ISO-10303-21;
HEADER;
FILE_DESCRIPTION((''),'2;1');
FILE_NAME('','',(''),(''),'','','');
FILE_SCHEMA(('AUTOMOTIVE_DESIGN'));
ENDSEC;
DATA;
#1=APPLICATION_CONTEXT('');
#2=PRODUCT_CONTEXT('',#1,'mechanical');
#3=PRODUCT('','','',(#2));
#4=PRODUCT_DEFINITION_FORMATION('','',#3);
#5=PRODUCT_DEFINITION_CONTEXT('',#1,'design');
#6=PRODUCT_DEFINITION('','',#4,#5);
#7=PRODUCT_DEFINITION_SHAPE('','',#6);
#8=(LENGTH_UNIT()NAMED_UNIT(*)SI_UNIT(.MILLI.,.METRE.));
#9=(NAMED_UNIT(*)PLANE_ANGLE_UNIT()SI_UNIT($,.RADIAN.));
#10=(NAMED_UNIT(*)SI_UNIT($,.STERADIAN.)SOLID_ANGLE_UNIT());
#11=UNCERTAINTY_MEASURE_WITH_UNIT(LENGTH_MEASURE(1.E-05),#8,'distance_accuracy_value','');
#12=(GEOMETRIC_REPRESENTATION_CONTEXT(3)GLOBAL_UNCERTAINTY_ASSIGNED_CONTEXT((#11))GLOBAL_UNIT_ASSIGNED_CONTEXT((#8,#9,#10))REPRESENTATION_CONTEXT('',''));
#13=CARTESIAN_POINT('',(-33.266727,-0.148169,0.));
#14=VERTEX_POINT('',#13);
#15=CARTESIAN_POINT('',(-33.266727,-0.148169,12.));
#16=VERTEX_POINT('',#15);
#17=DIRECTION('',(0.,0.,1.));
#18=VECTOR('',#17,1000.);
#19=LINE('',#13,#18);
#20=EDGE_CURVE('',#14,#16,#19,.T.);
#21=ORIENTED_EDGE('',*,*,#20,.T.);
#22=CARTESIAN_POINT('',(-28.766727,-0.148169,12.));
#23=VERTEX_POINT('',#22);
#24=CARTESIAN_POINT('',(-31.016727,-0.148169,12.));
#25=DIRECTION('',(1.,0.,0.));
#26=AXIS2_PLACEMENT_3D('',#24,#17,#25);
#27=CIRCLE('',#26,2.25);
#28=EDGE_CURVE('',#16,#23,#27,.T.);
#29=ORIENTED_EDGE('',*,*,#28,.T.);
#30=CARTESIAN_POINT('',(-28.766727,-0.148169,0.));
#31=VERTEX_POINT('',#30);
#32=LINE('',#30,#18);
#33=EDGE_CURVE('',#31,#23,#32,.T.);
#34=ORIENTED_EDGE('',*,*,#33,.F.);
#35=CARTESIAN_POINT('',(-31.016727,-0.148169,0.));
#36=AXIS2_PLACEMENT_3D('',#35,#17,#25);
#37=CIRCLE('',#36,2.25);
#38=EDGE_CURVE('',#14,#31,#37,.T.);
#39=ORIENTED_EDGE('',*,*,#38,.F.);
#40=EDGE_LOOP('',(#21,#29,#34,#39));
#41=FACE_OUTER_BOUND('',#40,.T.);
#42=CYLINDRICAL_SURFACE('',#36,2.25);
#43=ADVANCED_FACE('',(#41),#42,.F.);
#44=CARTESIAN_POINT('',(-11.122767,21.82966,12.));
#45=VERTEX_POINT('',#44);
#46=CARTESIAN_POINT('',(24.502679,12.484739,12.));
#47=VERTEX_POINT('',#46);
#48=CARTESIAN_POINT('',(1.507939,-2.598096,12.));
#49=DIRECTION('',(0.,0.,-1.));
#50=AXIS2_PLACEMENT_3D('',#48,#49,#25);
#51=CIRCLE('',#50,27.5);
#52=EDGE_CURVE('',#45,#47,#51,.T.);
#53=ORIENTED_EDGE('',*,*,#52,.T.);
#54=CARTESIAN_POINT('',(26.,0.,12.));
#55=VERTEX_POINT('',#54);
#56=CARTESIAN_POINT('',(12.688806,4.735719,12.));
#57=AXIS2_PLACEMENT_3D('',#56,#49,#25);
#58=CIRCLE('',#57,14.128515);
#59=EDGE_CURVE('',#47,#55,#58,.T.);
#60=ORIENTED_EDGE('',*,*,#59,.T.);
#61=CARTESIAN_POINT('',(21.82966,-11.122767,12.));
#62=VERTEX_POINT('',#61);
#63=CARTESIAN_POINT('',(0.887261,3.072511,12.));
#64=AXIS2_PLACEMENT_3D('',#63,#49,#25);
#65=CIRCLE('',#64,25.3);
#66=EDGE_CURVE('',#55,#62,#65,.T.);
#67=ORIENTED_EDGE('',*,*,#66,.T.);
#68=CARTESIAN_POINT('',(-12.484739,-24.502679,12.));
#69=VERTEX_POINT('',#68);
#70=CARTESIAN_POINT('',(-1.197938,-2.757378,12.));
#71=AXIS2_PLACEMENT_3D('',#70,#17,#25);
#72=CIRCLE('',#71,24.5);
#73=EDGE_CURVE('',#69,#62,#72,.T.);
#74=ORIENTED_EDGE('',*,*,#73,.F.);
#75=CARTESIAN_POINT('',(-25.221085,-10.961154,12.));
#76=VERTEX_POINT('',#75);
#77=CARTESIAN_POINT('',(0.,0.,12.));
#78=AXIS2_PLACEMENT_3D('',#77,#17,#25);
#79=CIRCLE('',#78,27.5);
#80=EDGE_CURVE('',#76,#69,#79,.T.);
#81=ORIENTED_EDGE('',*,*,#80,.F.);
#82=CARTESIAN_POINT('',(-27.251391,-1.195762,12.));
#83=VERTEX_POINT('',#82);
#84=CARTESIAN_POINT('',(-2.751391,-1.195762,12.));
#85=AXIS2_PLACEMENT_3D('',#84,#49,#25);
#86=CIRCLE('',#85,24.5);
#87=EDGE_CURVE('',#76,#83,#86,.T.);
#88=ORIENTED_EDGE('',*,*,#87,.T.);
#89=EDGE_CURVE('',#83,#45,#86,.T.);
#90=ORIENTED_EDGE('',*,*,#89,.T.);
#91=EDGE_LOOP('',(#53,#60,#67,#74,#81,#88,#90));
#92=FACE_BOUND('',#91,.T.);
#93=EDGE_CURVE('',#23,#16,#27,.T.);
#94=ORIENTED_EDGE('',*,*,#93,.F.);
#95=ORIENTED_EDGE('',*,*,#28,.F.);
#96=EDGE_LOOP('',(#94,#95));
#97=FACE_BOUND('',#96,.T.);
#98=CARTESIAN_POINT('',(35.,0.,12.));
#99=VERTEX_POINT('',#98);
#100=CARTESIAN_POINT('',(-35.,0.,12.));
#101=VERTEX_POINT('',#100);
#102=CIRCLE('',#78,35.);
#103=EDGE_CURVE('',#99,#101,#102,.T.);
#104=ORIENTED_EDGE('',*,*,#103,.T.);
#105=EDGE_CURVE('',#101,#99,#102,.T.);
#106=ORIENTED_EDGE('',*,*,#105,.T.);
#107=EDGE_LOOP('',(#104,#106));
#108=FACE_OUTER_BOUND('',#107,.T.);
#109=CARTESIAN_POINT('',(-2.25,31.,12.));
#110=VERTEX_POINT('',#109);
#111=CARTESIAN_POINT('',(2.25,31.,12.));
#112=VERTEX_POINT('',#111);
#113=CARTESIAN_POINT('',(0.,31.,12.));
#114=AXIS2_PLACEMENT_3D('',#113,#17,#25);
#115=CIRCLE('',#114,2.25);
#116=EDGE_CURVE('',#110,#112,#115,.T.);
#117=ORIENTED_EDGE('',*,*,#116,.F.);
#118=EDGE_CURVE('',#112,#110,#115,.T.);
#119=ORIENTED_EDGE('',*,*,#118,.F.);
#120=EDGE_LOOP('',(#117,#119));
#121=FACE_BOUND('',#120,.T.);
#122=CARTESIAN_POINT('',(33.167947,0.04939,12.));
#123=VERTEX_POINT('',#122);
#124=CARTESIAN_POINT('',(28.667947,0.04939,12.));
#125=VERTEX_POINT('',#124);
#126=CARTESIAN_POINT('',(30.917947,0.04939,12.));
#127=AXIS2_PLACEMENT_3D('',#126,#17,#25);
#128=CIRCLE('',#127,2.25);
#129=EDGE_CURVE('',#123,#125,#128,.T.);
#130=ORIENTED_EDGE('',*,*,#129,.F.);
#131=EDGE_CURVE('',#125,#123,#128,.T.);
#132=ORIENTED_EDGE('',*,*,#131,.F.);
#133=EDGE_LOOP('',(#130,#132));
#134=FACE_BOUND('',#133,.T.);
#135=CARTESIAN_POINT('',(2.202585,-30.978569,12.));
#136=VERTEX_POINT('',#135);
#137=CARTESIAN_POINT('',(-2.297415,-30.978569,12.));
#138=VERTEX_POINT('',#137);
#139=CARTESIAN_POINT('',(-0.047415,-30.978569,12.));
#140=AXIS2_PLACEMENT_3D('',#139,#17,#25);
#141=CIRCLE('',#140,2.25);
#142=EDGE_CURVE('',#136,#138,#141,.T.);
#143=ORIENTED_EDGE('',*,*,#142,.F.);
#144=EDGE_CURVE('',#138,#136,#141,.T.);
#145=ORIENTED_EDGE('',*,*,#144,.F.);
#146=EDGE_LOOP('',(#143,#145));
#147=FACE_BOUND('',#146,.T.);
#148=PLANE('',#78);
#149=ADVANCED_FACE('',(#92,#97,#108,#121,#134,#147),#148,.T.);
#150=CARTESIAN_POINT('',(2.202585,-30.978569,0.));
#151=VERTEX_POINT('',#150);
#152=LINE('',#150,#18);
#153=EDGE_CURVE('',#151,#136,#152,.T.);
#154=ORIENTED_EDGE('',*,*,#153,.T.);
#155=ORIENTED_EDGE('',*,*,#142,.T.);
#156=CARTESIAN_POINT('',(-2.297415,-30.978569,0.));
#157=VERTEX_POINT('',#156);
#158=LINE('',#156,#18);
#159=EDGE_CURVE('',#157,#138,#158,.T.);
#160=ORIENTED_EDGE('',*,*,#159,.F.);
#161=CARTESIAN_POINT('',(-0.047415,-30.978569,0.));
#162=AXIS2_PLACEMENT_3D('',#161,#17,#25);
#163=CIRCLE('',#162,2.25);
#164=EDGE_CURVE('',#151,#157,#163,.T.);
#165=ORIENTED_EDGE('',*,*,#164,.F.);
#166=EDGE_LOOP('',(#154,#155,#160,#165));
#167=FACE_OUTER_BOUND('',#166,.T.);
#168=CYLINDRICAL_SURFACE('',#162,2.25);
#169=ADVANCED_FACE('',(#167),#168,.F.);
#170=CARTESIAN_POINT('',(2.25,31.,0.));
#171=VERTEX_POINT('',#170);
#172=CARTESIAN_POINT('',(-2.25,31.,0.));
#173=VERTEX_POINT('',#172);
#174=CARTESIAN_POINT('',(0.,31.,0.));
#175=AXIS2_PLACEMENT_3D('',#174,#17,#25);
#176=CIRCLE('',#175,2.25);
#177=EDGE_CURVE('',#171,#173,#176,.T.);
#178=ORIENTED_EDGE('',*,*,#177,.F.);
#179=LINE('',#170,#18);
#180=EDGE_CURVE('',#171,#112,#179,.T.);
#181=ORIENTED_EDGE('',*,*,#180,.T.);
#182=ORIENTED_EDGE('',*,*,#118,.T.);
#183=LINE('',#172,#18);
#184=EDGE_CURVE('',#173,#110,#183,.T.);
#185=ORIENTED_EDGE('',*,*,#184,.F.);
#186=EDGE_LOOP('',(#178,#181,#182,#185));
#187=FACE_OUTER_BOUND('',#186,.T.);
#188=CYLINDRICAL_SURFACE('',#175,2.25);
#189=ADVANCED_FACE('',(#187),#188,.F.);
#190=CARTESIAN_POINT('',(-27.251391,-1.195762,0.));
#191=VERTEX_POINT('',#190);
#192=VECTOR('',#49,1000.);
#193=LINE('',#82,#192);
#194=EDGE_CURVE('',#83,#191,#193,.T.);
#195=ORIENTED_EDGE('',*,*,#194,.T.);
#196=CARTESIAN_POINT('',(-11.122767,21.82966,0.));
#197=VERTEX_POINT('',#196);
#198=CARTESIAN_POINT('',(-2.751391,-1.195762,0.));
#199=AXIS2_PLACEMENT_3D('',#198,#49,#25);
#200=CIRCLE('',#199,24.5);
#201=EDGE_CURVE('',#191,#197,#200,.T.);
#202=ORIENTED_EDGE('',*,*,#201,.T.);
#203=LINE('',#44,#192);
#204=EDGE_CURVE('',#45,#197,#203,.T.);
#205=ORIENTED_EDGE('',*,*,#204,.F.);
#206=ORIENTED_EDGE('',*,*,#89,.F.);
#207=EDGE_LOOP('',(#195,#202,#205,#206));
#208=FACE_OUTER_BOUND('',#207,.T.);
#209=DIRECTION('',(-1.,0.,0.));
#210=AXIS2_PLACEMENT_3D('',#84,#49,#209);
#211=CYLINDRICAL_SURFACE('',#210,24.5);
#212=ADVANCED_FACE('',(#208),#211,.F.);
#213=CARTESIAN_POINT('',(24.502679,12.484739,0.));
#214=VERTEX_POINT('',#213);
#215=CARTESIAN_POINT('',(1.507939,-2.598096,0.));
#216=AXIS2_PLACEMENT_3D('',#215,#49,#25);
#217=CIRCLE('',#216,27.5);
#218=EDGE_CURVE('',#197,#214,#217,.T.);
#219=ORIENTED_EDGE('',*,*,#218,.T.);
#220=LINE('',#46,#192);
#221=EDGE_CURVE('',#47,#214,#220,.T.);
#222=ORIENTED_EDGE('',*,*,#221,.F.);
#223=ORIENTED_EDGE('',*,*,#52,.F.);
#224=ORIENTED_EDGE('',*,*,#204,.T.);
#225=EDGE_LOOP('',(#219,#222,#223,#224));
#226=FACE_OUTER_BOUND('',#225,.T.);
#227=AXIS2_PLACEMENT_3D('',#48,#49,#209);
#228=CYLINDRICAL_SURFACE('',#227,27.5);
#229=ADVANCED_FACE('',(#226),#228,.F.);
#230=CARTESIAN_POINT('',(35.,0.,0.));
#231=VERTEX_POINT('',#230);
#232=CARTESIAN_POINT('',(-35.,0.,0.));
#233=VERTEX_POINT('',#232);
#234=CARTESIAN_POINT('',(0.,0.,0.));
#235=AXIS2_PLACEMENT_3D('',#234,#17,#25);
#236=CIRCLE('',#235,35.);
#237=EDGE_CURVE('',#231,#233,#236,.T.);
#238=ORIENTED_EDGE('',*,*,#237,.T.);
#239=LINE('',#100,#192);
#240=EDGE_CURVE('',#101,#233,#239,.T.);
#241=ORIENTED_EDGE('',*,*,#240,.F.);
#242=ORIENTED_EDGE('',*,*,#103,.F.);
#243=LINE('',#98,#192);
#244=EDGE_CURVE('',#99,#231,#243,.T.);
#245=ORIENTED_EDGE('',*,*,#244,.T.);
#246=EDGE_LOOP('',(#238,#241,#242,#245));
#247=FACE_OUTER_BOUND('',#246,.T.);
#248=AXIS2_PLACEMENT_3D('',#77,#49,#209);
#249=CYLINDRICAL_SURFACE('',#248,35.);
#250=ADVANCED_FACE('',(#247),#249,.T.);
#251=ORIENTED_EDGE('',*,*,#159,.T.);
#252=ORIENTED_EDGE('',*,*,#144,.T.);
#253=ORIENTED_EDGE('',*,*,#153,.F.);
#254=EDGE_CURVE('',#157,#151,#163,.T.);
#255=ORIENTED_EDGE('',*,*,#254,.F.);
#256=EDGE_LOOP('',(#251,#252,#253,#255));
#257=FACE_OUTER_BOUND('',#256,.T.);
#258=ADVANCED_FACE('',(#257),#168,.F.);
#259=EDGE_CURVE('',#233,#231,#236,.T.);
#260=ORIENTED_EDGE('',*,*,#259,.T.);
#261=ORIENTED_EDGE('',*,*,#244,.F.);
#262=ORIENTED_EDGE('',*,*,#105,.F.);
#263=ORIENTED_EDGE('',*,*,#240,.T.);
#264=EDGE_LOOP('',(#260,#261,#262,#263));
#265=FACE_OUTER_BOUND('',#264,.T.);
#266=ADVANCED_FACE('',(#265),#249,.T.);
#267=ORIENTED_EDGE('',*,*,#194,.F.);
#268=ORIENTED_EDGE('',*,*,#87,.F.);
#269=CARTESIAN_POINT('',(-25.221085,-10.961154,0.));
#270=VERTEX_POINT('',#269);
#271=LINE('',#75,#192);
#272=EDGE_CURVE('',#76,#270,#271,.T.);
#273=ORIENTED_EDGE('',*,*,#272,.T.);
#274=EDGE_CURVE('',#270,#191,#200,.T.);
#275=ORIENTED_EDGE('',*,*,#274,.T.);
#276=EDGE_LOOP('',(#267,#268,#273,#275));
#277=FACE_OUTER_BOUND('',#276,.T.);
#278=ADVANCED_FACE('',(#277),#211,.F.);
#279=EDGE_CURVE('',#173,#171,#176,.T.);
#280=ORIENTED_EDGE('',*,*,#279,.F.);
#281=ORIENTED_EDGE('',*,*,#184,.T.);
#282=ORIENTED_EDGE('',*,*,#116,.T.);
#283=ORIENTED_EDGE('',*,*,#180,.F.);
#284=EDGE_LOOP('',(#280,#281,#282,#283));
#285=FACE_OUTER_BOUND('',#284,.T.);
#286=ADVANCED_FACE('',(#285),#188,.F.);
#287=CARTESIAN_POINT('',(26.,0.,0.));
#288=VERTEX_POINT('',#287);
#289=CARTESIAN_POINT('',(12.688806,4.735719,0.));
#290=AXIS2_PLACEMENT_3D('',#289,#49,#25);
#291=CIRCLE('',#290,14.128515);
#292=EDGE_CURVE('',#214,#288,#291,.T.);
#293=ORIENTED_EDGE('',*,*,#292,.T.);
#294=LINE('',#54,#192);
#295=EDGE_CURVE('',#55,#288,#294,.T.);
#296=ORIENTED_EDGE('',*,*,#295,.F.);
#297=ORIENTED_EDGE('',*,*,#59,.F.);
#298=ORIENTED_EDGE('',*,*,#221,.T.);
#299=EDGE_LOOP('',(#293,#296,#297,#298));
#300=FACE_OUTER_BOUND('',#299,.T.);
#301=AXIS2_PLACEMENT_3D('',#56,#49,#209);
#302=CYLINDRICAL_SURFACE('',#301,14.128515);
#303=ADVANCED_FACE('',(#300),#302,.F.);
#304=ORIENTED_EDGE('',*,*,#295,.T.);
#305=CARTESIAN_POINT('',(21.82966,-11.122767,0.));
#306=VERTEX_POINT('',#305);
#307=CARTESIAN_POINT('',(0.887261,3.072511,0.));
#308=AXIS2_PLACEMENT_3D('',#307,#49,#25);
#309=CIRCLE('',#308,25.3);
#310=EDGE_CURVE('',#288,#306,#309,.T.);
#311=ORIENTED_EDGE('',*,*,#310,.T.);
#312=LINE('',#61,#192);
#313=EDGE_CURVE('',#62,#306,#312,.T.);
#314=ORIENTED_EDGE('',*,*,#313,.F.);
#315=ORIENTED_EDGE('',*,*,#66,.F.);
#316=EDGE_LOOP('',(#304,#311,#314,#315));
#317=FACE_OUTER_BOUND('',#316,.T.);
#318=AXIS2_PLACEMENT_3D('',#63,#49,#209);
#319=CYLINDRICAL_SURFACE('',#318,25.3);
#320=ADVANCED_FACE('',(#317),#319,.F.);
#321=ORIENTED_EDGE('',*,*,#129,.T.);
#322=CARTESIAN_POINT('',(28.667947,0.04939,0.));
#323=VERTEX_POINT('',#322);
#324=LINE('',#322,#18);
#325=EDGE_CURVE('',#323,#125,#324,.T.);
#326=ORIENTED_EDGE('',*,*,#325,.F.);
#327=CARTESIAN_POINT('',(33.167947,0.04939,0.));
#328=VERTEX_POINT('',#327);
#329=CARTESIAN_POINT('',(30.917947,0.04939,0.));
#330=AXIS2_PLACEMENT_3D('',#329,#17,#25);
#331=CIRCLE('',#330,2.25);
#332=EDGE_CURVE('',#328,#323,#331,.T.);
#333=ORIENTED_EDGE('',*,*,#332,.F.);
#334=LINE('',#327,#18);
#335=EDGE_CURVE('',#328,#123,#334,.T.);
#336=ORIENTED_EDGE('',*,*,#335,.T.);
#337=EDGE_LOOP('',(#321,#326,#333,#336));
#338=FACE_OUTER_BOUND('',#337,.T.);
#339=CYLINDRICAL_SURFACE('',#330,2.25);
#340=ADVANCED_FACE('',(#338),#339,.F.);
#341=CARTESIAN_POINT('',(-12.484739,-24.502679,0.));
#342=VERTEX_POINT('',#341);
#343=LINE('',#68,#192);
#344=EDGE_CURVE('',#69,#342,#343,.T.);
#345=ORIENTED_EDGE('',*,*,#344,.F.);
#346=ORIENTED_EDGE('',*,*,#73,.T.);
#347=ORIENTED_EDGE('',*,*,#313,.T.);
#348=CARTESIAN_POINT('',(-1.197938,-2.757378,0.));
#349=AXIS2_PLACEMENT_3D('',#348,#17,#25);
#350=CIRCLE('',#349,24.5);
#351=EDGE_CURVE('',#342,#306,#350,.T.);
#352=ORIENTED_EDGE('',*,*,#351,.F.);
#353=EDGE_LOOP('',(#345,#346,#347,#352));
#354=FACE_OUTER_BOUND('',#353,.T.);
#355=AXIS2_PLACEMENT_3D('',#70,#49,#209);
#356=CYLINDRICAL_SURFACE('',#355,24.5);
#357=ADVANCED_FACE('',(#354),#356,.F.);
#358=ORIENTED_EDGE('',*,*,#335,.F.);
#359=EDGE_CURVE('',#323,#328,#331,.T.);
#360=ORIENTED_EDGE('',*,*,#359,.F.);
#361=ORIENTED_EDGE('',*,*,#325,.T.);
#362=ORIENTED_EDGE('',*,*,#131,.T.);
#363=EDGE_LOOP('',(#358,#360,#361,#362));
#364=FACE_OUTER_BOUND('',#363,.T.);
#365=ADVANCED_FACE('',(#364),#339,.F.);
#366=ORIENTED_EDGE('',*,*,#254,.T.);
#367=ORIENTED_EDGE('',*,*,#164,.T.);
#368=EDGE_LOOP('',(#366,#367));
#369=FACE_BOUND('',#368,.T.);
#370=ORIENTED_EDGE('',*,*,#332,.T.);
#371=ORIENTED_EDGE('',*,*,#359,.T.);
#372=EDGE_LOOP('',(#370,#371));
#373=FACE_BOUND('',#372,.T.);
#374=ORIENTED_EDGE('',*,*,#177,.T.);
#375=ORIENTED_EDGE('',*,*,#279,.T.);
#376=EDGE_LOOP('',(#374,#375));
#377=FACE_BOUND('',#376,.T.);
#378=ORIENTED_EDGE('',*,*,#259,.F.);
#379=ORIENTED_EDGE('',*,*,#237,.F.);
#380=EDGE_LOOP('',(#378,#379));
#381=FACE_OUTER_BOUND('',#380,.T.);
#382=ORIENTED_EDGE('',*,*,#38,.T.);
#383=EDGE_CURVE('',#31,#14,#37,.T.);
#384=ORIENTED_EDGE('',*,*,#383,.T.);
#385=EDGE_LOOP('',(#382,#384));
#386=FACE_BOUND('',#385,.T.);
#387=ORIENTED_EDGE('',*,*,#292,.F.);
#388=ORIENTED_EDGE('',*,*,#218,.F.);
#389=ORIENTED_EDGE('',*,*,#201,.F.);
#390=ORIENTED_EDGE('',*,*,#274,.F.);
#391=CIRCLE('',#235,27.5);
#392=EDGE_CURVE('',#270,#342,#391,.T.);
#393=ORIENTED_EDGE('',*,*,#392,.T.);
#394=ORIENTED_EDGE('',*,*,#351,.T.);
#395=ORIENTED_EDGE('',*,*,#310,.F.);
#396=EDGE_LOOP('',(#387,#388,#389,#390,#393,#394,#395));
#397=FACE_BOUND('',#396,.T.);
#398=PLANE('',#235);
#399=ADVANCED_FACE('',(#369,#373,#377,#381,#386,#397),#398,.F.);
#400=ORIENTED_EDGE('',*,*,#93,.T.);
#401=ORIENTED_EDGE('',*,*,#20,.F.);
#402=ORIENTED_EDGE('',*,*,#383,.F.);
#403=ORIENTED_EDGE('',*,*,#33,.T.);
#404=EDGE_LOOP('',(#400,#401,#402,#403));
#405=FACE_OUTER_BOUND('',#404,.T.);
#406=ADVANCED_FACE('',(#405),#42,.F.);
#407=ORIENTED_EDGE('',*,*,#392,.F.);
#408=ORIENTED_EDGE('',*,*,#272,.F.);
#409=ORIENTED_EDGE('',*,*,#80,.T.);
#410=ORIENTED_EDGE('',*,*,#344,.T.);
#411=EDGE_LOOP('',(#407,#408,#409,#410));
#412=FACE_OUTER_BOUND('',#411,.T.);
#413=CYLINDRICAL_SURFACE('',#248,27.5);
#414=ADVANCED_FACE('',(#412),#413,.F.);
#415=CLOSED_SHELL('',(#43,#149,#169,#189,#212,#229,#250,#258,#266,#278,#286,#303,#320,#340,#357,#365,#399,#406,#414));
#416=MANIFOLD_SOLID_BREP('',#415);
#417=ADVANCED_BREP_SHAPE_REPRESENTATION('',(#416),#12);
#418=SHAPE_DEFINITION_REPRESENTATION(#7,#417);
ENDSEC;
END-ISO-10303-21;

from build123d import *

# Parameters (mm, degrees)
SKETCH_2_R          = 35
EXTRUDE_1_DEPTH     = 12
SKETCH_3_R          = 2.25
CUT_EXTRUDE_1_DEPTH = 51.931326313


with BuildPart() as part:
    # 草图2 → 凸台-拉伸1 (new body)
    with BuildSketch(Plane.XY):
        Circle(SKETCH_2_R)
        with BuildLine():
            ThreePointArc((-12.484738743, -24.502679415), (-20.031862375, -18.840766699), (-25.22108467, -10.961153593))
            ThreePointArc((-25.22108467, -10.961153593), (-25.259217651, 8.481414129), (-11.122767244, 21.829659843))
            ThreePointArc((-11.122767244, 21.829659843), (8.485416214, 24.001994273), (24.502679415, 12.484738743))
            ThreePointArc((24.502679415, 12.484738743), (26.716793299, 6.418124257), (26, 0))
            ThreePointArc((26, 0), (24.576877243, -5.809609847), (21.829659843, -11.122767244))
            ThreePointArc((21.829659843, -11.122767244), (9.253297944, -24.916386782), (-9.389722524, -25.847303746))
            ThreePointArc((-9.389722524, -25.847303746), (-10.960408212, -25.228341041), (-12.484738743, -24.502679415))
        make_face(mode=Mode.SUBTRACT)
    extrude(amount=EXTRUDE_1_DEPTH)

    # 草图3 → 切除-拉伸1 (cut, through all)
    with BuildSketch(Plane.XY.offset(12)):
        with Locations((0, 31)):
            Circle(SKETCH_3_R)
        with Locations((30.917947145, 0.049389692)):
            Circle(SKETCH_3_R)
        with Locations((-0.047414981, -30.978569044)):
            Circle(SKETCH_3_R)
        with Locations((-31.016726529, -0.148169076)):
            Circle(SKETCH_3_R)
    extrude(amount=-CUT_EXTRUDE_1_DEPTH, mode=Mode.SUBTRACT)


solid = part.part
